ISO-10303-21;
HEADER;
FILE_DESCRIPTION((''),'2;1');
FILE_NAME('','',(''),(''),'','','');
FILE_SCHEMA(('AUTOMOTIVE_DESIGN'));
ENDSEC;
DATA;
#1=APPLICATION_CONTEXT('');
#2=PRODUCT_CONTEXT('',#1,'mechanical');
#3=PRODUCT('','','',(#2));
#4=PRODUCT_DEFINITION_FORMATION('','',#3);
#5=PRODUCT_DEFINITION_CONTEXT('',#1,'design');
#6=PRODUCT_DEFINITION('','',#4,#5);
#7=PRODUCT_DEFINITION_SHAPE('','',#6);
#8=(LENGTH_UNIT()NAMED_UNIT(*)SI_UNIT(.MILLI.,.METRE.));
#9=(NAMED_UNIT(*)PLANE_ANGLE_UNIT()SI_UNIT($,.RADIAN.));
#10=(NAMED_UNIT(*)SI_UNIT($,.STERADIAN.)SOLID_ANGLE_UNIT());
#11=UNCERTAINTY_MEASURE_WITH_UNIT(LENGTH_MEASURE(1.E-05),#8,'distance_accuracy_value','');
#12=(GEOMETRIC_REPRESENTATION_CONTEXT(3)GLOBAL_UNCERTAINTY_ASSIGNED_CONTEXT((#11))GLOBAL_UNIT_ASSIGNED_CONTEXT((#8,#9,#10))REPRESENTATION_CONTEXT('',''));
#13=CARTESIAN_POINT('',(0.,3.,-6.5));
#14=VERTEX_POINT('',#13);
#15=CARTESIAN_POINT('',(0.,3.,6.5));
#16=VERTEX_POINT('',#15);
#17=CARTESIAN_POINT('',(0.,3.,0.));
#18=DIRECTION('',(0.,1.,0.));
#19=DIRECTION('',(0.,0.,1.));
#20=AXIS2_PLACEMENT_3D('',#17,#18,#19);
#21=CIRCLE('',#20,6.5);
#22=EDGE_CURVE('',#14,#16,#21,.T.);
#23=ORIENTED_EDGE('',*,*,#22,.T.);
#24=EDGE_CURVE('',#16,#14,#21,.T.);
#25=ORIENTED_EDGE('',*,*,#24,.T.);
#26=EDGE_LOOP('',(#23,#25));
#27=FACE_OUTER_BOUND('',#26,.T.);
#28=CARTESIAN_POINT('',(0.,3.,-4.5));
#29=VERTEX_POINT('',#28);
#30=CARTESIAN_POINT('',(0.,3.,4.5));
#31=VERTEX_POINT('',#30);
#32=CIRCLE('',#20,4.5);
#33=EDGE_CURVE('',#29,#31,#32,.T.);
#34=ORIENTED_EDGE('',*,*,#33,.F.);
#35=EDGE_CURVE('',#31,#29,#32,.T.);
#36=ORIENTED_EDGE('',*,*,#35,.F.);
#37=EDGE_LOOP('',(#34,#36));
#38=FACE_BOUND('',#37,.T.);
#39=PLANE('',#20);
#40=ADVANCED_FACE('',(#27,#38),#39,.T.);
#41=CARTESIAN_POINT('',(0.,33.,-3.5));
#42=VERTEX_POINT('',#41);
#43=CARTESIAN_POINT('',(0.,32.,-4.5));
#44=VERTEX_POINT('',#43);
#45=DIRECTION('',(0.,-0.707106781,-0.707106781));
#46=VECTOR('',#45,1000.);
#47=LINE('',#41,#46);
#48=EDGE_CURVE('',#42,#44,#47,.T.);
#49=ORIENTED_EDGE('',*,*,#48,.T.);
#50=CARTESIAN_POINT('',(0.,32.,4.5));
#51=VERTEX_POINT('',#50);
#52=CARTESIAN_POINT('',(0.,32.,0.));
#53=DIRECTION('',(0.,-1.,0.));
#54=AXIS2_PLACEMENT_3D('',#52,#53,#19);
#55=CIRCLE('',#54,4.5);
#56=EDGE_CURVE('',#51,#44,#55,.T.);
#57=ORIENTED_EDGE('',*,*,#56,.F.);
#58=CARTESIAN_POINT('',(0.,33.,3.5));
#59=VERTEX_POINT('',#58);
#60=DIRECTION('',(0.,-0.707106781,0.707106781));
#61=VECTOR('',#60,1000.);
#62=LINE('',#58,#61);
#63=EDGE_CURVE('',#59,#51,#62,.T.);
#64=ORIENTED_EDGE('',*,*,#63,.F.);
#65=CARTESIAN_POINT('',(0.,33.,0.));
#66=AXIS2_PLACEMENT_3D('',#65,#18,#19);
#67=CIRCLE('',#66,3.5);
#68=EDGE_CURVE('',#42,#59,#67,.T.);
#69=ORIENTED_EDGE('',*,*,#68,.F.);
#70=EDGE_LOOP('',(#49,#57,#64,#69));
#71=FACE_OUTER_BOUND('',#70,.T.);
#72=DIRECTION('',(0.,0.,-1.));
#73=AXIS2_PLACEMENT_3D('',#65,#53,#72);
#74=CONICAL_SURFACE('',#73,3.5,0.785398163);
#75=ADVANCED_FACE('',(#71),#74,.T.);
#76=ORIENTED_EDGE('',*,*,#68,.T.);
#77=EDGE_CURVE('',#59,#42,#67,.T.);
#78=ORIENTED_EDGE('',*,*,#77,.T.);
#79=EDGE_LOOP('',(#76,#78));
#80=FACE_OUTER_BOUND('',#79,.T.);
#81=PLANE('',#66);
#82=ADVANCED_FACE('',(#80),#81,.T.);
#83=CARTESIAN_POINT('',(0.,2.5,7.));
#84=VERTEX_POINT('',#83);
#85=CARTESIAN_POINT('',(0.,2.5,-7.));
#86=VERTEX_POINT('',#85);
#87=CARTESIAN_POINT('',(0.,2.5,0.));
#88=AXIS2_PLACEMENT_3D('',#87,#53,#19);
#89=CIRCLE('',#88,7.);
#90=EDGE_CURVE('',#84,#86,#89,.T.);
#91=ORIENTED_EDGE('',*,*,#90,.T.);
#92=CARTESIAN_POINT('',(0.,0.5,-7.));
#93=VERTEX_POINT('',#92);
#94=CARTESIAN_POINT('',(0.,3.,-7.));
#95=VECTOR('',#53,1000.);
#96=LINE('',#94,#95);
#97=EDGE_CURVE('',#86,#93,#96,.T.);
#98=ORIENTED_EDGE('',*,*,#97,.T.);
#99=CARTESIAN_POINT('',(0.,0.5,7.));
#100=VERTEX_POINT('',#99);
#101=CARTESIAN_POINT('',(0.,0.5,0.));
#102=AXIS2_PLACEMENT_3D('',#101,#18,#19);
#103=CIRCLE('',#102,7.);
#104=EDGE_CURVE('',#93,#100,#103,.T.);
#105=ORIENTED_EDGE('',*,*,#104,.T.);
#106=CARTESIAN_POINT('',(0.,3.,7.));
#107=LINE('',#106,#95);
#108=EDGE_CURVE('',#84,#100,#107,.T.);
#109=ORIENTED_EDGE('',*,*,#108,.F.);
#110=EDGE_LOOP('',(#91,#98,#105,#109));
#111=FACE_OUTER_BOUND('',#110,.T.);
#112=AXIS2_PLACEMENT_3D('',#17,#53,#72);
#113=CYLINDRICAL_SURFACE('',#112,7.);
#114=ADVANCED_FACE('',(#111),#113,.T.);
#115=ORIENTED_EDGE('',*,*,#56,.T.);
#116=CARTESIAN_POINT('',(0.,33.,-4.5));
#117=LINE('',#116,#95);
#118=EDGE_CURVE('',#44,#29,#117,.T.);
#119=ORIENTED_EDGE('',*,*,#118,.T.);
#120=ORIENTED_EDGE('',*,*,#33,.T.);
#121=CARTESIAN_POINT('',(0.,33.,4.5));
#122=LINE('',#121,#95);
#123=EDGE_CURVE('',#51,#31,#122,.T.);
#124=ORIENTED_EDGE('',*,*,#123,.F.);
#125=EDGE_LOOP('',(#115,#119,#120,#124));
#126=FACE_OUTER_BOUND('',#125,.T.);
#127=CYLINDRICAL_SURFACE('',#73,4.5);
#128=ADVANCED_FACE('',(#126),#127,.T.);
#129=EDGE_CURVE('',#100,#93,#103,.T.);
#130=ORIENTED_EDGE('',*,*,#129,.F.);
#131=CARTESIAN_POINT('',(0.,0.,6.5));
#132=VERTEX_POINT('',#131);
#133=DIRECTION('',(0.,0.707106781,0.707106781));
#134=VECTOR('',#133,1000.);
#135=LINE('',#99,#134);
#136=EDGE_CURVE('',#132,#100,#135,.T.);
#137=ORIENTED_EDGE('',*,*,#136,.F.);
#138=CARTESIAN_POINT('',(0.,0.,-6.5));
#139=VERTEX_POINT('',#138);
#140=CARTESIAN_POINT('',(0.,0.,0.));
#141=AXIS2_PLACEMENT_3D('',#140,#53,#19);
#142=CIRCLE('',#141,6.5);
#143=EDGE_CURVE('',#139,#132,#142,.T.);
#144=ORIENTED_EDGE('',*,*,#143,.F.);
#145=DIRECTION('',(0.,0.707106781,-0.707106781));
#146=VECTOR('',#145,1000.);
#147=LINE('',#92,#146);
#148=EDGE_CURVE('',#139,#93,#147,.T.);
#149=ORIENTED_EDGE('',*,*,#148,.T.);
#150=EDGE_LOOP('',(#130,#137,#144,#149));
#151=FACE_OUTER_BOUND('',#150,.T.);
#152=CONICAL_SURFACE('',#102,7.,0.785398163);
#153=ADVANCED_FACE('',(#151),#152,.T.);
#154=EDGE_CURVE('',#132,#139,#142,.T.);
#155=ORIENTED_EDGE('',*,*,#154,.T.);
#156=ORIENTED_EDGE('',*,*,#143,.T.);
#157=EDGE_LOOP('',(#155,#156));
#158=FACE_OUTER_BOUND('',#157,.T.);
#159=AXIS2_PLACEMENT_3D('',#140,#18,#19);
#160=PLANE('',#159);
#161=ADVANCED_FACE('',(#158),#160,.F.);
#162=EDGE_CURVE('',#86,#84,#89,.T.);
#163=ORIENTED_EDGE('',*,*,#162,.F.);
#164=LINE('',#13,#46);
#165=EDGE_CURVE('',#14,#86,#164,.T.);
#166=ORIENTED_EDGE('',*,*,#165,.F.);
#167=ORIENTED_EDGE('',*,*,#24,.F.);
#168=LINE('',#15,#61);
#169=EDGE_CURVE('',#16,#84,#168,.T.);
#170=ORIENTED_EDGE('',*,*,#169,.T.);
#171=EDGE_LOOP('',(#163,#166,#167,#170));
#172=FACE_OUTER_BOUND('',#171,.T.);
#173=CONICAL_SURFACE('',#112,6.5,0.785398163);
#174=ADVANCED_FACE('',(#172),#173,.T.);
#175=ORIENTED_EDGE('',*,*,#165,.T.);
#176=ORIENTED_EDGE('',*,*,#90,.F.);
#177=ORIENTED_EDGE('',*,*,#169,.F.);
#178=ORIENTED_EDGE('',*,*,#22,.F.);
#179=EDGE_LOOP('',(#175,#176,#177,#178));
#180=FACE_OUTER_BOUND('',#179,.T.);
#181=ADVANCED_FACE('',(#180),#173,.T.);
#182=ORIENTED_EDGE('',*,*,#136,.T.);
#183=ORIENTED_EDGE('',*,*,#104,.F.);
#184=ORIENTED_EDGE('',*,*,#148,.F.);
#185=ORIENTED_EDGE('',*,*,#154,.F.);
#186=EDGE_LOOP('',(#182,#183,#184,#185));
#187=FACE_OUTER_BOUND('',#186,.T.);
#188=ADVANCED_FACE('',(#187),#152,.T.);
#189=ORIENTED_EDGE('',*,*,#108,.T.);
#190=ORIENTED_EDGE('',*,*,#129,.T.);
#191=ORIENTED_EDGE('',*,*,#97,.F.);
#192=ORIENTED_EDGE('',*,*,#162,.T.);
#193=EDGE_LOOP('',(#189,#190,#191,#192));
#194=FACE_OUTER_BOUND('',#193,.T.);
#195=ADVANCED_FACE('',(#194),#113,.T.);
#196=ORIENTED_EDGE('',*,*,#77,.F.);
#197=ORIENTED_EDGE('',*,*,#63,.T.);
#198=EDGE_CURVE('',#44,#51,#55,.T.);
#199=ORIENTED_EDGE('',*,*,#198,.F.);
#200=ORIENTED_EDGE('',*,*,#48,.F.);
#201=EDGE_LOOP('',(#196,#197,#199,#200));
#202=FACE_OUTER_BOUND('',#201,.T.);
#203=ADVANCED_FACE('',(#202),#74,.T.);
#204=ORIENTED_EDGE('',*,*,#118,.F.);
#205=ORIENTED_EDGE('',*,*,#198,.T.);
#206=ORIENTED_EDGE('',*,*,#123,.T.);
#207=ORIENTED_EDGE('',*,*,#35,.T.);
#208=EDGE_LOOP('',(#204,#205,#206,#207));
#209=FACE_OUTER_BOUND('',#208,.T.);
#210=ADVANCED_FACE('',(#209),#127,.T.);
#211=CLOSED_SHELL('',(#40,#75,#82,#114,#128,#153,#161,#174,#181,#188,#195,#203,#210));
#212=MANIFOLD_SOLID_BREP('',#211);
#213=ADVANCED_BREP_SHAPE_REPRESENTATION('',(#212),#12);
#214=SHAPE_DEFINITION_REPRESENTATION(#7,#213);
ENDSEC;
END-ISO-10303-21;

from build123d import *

# Parameters (mm, degrees)
SKETCH1_R           = 7
BOSS_EXTRUDE1_DEPTH = 3
SKETCH2_R           = 4.5
BOSS_EXTRUDE2_DEPTH = 30
CHAMFER1_SIZE       = 1
CHAMFER2_SIZE       = 0.5


with BuildPart() as part:
    # Sketch1 → Boss-Extrude1 (new body)
    with BuildSketch(Plane(origin=(0, 0, 0), x_dir=(1, 0, 0), z_dir=(0, 1, 0))):
        with Locations(Location((0, 0, 0), (0, 0, 270))):
            Circle(SKETCH1_R)
    extrude(amount=BOSS_EXTRUDE1_DEPTH)

    # Sketch2 → Boss-Extrude2 (add)
    with BuildSketch(Plane(origin=(0, 3, 0), x_dir=(1, 0, 0), z_dir=(0, 1, 0))):
        with Locations(Location((0, 0, 0), (0, 0, 270))):
            Circle(SKETCH2_R)
    extrude(amount=BOSS_EXTRUDE2_DEPTH)

    # Chamfer1
    chamfer1_edges = [part.edges().sort_by_distance(p)[0] for p in [
        (0, 33, -4.5),
    ]]
    chamfer(chamfer1_edges, length=CHAMFER1_SIZE)

    # Chamfer2
    chamfer2_edges = [part.edges().sort_by_distance(p)[0] for p in [
        (0, 0, -7),
        (0, 3, -7),
    ]]
    chamfer(chamfer2_edges, length=CHAMFER2_SIZE)


solid = part.part
